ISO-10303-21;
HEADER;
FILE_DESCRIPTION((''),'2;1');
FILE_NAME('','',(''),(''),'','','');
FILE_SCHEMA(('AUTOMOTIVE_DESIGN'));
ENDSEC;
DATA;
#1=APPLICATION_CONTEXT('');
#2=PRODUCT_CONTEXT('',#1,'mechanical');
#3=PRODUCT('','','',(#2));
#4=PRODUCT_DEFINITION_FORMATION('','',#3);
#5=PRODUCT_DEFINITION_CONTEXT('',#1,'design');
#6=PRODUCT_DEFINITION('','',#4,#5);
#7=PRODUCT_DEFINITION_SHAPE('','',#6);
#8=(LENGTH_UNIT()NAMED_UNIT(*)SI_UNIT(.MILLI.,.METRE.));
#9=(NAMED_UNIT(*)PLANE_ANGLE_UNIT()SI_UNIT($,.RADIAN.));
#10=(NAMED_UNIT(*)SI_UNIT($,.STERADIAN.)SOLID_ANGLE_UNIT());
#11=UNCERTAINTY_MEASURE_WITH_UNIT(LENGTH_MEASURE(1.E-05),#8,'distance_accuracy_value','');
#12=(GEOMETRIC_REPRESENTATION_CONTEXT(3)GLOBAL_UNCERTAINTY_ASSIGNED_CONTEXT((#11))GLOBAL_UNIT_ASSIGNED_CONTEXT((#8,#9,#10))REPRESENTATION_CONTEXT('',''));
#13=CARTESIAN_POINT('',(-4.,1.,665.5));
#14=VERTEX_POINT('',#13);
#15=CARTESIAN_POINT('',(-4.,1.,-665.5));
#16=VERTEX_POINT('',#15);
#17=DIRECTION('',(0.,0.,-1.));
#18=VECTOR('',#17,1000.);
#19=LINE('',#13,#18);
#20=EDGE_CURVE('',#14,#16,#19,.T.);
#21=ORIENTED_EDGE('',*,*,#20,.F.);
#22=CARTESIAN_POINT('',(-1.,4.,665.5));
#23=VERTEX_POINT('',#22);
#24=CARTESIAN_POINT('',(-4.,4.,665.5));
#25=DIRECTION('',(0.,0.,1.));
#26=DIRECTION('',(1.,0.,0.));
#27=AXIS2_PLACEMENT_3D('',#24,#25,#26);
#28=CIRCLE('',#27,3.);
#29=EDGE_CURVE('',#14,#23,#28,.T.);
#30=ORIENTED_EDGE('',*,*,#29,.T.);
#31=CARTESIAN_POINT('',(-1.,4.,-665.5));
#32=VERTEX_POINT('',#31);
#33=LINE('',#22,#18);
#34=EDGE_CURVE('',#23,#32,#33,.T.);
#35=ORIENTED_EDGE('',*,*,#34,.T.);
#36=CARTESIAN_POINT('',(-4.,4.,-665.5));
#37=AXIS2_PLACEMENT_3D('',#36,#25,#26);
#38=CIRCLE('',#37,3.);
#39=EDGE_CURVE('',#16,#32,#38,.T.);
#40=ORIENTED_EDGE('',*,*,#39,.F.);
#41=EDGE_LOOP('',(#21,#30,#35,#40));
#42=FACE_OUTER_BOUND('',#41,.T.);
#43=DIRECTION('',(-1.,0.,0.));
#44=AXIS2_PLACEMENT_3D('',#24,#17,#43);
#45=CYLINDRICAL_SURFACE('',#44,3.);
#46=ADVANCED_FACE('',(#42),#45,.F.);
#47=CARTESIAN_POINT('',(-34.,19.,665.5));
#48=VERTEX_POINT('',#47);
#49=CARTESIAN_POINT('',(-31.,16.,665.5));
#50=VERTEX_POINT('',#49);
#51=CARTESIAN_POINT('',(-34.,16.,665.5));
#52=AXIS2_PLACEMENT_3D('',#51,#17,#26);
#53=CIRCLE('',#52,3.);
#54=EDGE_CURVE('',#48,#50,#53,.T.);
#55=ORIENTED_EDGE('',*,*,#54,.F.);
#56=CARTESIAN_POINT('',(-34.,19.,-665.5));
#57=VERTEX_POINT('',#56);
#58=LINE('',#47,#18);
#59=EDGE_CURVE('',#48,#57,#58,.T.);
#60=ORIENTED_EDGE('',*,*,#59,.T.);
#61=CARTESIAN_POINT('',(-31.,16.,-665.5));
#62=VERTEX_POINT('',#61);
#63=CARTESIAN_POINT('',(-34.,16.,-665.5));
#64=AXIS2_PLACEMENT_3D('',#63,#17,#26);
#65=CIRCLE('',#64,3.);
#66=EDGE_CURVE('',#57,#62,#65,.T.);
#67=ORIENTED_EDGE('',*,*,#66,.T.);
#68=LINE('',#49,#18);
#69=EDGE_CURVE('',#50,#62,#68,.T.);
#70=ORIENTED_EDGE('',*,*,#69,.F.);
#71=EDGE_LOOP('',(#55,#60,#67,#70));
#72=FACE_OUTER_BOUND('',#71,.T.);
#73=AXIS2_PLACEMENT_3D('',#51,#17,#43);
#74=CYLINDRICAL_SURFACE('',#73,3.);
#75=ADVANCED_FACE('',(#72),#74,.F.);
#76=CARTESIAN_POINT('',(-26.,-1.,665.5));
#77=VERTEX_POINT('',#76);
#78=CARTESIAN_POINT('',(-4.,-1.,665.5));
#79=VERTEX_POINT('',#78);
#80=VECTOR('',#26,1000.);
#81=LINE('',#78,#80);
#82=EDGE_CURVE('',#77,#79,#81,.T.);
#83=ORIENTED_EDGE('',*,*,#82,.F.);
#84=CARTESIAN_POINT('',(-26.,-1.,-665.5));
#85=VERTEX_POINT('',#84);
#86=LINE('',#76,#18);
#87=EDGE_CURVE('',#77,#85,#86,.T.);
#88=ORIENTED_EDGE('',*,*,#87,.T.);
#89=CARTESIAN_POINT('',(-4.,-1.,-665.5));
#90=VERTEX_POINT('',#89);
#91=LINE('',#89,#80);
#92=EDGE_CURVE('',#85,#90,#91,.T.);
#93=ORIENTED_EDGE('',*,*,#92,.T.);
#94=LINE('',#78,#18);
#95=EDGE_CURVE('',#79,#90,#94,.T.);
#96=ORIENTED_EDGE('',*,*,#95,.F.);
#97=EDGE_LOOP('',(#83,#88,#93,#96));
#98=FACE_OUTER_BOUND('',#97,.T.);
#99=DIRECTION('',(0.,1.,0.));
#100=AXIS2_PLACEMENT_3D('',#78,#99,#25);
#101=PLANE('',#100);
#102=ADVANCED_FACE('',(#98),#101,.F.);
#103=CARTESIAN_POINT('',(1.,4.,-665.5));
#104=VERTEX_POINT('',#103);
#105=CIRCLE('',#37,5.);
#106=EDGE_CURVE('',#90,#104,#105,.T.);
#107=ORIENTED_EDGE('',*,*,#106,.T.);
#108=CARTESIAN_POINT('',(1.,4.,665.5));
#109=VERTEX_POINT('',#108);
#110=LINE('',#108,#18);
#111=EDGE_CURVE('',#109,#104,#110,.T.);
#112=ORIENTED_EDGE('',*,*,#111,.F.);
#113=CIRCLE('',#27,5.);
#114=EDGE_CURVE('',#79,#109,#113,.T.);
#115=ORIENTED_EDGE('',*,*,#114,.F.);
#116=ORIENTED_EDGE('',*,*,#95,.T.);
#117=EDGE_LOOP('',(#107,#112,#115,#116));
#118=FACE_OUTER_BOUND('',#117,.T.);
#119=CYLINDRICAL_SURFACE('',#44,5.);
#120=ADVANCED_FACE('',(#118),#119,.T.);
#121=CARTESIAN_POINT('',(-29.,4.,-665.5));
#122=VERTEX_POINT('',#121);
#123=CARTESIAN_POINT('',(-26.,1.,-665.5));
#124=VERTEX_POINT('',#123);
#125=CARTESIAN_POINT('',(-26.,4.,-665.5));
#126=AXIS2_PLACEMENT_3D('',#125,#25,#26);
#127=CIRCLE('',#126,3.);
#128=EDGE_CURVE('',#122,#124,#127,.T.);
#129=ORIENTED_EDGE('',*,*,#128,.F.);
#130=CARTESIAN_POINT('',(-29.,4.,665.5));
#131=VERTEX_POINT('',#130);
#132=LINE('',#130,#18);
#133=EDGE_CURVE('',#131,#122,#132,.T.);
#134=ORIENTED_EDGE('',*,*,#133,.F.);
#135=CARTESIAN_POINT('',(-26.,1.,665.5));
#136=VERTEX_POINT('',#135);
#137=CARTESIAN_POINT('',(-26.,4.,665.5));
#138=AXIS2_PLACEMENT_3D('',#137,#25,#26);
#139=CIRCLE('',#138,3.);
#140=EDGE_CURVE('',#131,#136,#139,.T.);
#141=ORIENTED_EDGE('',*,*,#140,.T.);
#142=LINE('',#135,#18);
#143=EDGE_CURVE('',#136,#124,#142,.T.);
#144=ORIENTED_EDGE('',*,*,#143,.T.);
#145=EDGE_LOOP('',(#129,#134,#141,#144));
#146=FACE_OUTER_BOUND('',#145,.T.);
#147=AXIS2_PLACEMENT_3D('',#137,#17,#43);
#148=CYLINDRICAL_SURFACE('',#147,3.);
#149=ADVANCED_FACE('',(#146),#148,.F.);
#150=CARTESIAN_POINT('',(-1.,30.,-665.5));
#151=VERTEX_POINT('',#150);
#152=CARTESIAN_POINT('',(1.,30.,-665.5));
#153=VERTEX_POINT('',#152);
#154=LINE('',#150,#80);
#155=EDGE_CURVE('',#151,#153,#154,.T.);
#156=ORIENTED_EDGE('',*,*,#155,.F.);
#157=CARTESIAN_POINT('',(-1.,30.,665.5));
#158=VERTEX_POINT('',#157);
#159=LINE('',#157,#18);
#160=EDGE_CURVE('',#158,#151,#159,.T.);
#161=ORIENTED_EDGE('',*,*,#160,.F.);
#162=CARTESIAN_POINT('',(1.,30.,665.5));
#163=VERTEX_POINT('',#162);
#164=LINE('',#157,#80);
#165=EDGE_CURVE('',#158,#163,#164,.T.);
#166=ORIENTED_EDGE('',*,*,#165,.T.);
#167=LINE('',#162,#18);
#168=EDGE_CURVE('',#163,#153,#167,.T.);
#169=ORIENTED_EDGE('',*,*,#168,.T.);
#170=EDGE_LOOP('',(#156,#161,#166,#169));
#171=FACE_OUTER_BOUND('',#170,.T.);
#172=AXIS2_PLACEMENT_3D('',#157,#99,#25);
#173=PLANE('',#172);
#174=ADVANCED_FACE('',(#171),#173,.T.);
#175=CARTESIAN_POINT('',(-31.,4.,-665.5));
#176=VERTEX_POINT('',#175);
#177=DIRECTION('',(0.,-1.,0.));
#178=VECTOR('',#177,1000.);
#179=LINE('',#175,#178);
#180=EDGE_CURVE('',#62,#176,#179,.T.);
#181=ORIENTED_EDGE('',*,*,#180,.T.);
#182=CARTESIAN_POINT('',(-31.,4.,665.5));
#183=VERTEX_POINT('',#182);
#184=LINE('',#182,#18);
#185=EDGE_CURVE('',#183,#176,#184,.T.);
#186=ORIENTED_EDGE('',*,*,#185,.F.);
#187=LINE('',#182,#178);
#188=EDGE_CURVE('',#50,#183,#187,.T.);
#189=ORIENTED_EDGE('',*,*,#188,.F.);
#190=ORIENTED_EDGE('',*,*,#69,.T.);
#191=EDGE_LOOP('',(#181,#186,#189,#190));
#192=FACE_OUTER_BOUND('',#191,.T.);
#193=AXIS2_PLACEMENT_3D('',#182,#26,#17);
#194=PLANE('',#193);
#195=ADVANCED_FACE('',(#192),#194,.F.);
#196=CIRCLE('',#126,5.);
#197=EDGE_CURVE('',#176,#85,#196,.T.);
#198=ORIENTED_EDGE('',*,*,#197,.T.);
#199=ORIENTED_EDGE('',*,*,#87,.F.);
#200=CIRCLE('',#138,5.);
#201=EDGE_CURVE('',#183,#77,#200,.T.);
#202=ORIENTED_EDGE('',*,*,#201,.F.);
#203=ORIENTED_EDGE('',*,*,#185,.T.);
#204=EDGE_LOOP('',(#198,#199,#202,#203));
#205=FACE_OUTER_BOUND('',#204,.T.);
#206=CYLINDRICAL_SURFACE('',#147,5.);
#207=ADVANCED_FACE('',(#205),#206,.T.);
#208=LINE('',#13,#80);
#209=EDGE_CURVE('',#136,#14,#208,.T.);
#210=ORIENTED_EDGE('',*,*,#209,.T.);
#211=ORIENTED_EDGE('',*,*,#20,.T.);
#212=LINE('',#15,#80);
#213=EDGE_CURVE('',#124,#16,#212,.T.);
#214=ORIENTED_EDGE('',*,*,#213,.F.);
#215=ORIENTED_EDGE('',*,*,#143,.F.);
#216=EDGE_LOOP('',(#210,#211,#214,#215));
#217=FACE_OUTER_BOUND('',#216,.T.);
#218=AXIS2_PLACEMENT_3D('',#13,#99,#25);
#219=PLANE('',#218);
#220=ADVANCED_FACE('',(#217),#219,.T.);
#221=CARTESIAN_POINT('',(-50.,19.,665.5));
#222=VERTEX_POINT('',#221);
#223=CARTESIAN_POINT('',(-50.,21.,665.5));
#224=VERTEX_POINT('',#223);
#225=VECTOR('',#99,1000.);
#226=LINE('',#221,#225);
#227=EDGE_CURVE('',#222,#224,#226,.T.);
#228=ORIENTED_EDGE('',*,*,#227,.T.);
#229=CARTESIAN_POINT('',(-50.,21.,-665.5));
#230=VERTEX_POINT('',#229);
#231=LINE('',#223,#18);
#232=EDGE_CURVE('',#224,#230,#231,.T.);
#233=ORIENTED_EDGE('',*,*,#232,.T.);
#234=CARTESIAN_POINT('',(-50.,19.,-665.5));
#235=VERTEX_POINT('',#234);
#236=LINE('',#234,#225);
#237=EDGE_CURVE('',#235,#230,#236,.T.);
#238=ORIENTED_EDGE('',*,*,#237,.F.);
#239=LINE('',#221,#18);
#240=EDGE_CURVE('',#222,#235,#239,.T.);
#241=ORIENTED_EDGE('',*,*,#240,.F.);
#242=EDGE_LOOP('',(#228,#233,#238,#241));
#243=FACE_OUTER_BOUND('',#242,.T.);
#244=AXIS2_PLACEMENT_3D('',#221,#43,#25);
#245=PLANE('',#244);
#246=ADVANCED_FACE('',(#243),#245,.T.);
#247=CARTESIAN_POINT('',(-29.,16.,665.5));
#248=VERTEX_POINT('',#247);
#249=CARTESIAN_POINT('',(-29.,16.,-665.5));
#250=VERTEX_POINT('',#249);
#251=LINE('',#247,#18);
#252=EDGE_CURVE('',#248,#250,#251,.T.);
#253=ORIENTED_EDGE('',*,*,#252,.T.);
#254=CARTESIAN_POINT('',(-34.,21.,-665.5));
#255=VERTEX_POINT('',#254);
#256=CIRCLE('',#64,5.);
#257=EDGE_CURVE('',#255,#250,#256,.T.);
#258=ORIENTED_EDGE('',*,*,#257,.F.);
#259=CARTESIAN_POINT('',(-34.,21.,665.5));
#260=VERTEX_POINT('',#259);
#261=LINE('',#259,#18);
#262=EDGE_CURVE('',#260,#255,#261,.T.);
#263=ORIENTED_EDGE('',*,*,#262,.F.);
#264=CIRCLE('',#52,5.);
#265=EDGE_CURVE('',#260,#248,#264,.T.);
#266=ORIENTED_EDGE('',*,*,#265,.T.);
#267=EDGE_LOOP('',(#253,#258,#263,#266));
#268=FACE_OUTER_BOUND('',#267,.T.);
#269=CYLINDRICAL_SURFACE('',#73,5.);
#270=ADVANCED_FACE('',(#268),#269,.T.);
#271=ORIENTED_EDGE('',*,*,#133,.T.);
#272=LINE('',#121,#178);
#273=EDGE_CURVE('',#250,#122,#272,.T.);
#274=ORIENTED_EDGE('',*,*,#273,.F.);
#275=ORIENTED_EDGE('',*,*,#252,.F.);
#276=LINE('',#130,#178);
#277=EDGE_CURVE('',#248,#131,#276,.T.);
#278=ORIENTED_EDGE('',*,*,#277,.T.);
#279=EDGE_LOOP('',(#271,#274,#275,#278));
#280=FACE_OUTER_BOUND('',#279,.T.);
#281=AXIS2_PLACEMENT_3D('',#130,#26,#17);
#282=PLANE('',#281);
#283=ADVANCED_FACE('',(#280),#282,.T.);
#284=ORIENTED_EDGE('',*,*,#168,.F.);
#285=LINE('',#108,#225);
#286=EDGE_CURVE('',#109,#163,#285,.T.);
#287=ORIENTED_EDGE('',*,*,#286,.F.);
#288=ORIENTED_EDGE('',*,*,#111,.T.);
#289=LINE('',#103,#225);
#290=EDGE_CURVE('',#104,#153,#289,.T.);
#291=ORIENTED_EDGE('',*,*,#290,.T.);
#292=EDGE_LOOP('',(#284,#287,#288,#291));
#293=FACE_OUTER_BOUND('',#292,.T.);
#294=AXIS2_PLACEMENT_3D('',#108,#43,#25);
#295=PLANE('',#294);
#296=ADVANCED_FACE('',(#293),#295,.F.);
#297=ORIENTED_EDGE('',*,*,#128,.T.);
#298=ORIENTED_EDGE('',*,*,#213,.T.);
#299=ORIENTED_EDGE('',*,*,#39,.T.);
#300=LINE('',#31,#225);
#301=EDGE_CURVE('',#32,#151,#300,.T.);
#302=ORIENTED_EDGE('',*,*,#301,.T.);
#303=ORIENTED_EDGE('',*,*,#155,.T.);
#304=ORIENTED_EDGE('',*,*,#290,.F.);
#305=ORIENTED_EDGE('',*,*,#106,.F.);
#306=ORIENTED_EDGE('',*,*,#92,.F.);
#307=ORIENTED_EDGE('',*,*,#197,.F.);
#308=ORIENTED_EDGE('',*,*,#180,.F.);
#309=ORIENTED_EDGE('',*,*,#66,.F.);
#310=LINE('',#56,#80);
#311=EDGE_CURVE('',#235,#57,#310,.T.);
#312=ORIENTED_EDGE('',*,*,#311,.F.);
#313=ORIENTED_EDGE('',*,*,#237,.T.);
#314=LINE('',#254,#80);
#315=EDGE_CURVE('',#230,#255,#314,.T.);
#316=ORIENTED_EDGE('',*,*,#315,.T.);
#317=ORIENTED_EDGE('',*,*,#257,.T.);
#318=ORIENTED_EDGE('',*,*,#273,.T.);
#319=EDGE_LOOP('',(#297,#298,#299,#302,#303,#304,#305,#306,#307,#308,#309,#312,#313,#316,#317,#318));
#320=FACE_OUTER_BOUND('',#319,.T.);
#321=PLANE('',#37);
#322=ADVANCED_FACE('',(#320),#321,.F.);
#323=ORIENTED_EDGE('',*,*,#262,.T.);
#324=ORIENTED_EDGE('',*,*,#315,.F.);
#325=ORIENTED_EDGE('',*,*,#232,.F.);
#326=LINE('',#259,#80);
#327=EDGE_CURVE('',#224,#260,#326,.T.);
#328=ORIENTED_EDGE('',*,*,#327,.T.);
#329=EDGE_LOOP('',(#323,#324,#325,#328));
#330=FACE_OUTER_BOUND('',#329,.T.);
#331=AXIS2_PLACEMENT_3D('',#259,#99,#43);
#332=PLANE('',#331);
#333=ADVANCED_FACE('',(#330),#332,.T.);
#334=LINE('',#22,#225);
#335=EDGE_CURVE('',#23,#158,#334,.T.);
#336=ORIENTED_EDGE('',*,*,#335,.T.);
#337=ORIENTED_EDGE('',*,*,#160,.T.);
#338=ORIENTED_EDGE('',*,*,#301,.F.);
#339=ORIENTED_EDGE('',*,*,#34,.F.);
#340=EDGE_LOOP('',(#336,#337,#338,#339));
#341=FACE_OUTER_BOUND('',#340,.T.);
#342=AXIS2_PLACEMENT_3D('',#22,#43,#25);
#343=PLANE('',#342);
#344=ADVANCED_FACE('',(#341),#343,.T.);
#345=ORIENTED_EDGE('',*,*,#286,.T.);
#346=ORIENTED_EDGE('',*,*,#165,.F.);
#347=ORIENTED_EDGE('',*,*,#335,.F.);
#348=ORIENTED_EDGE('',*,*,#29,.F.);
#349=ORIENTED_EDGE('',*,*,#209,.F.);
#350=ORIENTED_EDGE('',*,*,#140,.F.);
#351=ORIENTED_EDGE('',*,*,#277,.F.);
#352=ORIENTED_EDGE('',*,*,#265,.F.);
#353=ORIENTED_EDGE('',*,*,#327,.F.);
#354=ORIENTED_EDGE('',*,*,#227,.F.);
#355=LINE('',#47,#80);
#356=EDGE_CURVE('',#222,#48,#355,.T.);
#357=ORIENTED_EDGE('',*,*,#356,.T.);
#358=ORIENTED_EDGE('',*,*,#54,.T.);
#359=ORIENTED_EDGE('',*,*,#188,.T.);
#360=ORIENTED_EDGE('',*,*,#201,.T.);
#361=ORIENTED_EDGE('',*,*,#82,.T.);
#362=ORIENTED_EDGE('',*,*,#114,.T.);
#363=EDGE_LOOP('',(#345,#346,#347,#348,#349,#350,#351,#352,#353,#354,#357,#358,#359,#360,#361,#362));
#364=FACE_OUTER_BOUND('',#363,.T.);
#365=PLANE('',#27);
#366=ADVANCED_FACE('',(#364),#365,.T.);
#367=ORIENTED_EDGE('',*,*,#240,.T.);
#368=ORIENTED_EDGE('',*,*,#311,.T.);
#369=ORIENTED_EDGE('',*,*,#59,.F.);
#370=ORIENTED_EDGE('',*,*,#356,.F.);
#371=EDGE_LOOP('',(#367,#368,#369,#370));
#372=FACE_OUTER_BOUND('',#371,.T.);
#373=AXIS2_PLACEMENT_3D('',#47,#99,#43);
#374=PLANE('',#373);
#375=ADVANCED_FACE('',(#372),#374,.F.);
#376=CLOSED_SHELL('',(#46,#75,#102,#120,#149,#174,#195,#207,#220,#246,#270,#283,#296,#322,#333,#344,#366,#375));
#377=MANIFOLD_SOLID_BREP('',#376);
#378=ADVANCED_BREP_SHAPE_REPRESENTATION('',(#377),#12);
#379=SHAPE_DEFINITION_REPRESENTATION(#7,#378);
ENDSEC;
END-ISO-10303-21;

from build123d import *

# Parameters (mm, degrees)
EXTRUDE_1_DEPTH = 665.5


with BuildPart() as part:
    # 草图1 → 拉伸-薄壁1 (new, symmetric)
    with BuildSketch(Plane.XY):
        with BuildLine():
            Line((-1, 30), (-1, 4))
            ThreePointArc((-1, 4), (-1.878679656, 1.878679656), (-4, 1))
            Line((-4, 1), (-26, 1))
            ThreePointArc((-26, 1), (-28.121320344, 1.878679656), (-29, 4))
            Line((-29, 4), (-29, 16))
            ThreePointArc((-29, 16), (-30.464466094, 19.535533906), (-34, 21))
            Line((-34, 21), (-50, 21))
            Line((-50, 21), (-50, 19))
            Line((-50, 19), (-34, 19))
            ThreePointArc((-34, 19), (-31.878679656, 18.121320344), (-31, 16))
            Line((-31, 16), (-31, 4))
            ThreePointArc((-31, 4), (-29.535533906, 0.464466094), (-26, -1))
            Line((-26, -1), (-4, -1))
            ThreePointArc((-4, -1), (-0.464466094, 0.464466094), (1, 4))
            Line((1, 4), (1, 30))
            Line((1, 30), (-1, 30))
        make_face()
    extrude(amount=EXTRUDE_1_DEPTH, both=True)


solid = part.part
